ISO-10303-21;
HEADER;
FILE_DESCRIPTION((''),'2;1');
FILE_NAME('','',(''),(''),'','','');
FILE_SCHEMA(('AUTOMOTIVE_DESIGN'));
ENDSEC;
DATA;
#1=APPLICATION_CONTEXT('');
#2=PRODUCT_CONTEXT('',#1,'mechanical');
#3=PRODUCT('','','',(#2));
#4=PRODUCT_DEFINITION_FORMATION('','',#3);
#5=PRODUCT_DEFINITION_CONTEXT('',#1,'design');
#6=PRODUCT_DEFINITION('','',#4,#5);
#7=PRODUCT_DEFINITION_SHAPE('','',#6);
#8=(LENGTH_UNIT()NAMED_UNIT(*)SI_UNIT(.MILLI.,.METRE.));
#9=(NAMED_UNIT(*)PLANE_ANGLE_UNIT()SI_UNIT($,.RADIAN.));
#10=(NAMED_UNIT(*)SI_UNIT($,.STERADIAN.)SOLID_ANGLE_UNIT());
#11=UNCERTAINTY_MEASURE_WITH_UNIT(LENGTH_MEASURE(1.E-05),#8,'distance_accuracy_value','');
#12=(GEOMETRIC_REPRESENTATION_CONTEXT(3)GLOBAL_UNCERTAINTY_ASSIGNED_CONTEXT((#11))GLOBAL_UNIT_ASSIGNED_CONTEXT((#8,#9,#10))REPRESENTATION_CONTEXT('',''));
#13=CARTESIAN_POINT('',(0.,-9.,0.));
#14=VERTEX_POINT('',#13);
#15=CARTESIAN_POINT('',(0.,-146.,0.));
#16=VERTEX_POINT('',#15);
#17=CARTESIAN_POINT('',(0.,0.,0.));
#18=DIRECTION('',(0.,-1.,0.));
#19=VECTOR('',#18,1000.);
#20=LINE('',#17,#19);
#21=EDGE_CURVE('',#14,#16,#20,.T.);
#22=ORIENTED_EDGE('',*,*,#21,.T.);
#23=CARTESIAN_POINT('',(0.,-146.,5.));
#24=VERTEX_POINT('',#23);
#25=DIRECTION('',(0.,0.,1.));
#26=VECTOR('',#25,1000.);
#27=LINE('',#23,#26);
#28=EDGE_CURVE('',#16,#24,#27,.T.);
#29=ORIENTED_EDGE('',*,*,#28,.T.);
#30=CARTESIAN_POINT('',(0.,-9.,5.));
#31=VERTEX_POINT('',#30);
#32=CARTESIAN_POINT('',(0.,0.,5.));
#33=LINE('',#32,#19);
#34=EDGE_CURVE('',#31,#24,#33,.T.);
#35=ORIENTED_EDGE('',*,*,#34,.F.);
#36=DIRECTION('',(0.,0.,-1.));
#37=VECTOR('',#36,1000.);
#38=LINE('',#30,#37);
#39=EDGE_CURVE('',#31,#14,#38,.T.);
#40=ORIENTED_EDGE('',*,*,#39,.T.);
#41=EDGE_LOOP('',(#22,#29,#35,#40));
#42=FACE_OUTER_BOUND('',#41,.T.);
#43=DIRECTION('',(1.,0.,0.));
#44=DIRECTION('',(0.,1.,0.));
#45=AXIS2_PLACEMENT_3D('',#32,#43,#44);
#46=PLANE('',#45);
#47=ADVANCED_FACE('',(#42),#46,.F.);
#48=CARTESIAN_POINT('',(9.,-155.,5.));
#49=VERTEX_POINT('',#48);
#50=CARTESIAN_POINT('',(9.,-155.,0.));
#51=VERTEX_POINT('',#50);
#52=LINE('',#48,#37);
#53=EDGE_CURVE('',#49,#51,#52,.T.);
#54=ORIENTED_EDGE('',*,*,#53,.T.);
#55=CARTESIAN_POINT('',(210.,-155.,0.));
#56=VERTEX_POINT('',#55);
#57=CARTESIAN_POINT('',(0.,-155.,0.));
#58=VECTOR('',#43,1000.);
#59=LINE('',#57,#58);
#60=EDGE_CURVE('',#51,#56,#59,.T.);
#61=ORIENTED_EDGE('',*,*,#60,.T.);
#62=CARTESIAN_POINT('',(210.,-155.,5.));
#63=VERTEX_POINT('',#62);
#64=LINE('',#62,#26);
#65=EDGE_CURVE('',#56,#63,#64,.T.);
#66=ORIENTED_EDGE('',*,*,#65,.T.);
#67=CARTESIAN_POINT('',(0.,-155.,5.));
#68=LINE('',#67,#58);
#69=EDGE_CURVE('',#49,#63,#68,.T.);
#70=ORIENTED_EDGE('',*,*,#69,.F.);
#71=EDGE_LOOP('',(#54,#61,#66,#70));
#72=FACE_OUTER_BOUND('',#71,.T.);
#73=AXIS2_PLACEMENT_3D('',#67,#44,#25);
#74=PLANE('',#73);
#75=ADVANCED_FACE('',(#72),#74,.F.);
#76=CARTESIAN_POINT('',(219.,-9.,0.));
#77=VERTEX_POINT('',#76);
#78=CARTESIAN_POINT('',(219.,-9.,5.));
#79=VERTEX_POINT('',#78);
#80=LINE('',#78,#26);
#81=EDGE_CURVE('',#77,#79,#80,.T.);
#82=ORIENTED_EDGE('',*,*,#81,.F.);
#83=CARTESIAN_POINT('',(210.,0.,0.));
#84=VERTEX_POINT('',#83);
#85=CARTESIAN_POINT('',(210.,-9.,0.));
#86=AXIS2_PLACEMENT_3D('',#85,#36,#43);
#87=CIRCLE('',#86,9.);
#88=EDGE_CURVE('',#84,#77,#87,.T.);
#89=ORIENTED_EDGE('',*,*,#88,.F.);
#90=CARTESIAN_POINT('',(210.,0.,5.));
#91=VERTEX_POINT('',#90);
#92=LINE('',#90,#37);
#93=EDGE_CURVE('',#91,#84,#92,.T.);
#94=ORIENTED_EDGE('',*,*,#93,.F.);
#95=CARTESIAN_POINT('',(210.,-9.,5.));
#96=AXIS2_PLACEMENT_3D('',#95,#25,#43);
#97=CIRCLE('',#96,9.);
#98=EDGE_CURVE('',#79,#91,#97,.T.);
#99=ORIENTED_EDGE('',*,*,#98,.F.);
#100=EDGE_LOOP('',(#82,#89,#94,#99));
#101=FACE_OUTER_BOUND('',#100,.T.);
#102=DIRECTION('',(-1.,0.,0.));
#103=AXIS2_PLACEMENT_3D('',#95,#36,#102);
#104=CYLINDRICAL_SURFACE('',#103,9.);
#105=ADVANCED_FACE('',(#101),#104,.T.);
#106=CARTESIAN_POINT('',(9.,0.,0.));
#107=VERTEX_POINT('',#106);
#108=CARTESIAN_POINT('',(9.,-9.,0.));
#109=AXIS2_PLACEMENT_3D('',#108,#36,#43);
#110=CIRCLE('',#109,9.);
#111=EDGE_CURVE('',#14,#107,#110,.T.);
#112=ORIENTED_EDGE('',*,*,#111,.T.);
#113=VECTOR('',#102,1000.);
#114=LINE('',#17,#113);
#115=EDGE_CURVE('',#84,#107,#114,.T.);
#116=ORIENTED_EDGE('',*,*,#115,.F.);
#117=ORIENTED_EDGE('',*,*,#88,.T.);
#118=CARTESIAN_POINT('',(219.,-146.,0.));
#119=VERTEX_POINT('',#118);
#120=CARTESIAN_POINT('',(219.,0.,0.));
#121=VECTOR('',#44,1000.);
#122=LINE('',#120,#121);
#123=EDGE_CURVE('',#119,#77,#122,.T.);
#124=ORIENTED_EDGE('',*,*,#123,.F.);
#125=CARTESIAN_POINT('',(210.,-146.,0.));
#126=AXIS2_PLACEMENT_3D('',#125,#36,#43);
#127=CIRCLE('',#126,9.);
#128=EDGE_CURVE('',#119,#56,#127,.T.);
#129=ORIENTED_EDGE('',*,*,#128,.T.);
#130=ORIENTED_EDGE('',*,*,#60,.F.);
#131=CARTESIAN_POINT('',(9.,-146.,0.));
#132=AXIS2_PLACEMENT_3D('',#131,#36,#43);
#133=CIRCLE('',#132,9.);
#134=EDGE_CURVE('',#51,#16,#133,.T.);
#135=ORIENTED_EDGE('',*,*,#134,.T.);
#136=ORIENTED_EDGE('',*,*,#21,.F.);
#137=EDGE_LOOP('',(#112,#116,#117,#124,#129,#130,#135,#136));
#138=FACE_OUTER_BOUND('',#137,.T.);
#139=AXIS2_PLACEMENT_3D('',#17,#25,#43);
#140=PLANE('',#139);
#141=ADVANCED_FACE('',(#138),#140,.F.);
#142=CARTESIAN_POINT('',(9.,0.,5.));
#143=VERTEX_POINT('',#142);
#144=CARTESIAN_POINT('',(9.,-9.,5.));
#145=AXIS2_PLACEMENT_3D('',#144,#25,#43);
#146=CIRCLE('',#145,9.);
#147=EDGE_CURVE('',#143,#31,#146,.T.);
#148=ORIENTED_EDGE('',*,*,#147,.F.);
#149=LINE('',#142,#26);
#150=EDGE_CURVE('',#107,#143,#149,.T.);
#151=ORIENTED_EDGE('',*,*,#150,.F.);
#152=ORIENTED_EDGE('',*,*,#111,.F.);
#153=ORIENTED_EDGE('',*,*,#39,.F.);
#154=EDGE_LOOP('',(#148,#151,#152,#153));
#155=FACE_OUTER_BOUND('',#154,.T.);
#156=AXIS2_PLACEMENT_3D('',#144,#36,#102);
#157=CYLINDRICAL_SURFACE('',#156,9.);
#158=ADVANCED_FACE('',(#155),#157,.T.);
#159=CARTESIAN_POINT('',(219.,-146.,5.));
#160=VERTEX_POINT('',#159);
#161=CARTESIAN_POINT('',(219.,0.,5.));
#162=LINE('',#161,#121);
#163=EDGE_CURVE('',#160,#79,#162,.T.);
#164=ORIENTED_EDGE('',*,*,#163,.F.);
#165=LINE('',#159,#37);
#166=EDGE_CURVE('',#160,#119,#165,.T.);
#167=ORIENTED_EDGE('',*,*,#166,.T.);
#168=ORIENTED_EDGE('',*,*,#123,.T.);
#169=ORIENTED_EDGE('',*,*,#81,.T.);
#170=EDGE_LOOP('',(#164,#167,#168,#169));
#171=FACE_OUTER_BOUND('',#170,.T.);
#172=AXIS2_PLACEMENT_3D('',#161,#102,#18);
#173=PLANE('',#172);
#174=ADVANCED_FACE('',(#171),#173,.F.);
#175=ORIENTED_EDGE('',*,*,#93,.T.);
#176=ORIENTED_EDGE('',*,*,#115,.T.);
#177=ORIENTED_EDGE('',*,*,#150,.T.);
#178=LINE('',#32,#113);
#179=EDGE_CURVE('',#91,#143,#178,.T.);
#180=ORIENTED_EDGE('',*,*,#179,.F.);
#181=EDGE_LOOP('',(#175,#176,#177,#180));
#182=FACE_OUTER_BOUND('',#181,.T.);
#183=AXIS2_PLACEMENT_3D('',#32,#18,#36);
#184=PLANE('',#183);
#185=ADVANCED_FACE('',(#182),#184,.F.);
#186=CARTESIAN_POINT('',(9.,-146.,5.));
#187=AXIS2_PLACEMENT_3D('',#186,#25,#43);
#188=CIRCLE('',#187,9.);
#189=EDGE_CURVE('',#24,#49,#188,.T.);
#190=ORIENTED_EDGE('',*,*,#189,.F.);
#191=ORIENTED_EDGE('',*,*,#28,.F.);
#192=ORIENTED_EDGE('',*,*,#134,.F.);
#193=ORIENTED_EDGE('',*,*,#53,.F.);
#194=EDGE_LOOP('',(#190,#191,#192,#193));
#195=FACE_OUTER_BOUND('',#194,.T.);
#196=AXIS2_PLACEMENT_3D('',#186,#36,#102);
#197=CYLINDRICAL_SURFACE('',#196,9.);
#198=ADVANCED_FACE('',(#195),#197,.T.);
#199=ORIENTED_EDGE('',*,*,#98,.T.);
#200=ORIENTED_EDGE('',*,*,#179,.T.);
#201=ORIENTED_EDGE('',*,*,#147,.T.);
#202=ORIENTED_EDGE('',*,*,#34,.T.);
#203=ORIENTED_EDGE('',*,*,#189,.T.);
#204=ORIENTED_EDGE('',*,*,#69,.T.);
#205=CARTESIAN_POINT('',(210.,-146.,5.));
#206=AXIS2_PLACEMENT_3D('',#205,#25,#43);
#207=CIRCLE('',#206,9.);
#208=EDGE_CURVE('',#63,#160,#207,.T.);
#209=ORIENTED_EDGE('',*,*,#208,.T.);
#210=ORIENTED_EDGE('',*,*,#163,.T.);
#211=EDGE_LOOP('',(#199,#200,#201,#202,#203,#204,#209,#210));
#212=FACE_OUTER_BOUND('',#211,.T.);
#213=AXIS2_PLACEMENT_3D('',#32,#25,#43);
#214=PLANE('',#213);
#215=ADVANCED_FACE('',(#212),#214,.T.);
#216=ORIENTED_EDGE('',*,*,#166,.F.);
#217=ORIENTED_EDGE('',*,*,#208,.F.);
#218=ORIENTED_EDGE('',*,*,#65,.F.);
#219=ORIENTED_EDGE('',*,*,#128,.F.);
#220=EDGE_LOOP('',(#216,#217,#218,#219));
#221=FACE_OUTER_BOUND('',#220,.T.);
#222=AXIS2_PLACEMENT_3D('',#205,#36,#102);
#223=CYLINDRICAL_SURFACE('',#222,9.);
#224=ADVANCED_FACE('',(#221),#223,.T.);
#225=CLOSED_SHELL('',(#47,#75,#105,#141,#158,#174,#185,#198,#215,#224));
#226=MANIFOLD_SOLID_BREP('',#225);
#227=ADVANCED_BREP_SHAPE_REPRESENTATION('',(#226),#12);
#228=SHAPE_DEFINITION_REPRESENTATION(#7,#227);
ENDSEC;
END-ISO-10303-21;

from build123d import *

# Parameters (mm, degrees)
SKETCH1_W           = 219
SKETCH1_H           = 155
BOSS_EXTRUDE1_DEPTH = 5
FILLET1_R           = 9


with BuildPart() as part:
    # Sketch1 → Boss-Extrude1 (new body)
    with BuildSketch(Plane.XY):
        with Locations((109.5, -77.5)):
            Rectangle(SKETCH1_W, SKETCH1_H)
    extrude(amount=BOSS_EXTRUDE1_DEPTH)

    # Fillet1
    fillet1_edges = [part.edges().sort_by_distance(p)[0] for p in [
        (0, 0, 2.5),
        (219, 0, 2.5),
        (219, -155, 2.5),
        (0, -155, 2.5),
    ]]
    fillet(fillet1_edges, radius=FILLET1_R)


solid = part.part
